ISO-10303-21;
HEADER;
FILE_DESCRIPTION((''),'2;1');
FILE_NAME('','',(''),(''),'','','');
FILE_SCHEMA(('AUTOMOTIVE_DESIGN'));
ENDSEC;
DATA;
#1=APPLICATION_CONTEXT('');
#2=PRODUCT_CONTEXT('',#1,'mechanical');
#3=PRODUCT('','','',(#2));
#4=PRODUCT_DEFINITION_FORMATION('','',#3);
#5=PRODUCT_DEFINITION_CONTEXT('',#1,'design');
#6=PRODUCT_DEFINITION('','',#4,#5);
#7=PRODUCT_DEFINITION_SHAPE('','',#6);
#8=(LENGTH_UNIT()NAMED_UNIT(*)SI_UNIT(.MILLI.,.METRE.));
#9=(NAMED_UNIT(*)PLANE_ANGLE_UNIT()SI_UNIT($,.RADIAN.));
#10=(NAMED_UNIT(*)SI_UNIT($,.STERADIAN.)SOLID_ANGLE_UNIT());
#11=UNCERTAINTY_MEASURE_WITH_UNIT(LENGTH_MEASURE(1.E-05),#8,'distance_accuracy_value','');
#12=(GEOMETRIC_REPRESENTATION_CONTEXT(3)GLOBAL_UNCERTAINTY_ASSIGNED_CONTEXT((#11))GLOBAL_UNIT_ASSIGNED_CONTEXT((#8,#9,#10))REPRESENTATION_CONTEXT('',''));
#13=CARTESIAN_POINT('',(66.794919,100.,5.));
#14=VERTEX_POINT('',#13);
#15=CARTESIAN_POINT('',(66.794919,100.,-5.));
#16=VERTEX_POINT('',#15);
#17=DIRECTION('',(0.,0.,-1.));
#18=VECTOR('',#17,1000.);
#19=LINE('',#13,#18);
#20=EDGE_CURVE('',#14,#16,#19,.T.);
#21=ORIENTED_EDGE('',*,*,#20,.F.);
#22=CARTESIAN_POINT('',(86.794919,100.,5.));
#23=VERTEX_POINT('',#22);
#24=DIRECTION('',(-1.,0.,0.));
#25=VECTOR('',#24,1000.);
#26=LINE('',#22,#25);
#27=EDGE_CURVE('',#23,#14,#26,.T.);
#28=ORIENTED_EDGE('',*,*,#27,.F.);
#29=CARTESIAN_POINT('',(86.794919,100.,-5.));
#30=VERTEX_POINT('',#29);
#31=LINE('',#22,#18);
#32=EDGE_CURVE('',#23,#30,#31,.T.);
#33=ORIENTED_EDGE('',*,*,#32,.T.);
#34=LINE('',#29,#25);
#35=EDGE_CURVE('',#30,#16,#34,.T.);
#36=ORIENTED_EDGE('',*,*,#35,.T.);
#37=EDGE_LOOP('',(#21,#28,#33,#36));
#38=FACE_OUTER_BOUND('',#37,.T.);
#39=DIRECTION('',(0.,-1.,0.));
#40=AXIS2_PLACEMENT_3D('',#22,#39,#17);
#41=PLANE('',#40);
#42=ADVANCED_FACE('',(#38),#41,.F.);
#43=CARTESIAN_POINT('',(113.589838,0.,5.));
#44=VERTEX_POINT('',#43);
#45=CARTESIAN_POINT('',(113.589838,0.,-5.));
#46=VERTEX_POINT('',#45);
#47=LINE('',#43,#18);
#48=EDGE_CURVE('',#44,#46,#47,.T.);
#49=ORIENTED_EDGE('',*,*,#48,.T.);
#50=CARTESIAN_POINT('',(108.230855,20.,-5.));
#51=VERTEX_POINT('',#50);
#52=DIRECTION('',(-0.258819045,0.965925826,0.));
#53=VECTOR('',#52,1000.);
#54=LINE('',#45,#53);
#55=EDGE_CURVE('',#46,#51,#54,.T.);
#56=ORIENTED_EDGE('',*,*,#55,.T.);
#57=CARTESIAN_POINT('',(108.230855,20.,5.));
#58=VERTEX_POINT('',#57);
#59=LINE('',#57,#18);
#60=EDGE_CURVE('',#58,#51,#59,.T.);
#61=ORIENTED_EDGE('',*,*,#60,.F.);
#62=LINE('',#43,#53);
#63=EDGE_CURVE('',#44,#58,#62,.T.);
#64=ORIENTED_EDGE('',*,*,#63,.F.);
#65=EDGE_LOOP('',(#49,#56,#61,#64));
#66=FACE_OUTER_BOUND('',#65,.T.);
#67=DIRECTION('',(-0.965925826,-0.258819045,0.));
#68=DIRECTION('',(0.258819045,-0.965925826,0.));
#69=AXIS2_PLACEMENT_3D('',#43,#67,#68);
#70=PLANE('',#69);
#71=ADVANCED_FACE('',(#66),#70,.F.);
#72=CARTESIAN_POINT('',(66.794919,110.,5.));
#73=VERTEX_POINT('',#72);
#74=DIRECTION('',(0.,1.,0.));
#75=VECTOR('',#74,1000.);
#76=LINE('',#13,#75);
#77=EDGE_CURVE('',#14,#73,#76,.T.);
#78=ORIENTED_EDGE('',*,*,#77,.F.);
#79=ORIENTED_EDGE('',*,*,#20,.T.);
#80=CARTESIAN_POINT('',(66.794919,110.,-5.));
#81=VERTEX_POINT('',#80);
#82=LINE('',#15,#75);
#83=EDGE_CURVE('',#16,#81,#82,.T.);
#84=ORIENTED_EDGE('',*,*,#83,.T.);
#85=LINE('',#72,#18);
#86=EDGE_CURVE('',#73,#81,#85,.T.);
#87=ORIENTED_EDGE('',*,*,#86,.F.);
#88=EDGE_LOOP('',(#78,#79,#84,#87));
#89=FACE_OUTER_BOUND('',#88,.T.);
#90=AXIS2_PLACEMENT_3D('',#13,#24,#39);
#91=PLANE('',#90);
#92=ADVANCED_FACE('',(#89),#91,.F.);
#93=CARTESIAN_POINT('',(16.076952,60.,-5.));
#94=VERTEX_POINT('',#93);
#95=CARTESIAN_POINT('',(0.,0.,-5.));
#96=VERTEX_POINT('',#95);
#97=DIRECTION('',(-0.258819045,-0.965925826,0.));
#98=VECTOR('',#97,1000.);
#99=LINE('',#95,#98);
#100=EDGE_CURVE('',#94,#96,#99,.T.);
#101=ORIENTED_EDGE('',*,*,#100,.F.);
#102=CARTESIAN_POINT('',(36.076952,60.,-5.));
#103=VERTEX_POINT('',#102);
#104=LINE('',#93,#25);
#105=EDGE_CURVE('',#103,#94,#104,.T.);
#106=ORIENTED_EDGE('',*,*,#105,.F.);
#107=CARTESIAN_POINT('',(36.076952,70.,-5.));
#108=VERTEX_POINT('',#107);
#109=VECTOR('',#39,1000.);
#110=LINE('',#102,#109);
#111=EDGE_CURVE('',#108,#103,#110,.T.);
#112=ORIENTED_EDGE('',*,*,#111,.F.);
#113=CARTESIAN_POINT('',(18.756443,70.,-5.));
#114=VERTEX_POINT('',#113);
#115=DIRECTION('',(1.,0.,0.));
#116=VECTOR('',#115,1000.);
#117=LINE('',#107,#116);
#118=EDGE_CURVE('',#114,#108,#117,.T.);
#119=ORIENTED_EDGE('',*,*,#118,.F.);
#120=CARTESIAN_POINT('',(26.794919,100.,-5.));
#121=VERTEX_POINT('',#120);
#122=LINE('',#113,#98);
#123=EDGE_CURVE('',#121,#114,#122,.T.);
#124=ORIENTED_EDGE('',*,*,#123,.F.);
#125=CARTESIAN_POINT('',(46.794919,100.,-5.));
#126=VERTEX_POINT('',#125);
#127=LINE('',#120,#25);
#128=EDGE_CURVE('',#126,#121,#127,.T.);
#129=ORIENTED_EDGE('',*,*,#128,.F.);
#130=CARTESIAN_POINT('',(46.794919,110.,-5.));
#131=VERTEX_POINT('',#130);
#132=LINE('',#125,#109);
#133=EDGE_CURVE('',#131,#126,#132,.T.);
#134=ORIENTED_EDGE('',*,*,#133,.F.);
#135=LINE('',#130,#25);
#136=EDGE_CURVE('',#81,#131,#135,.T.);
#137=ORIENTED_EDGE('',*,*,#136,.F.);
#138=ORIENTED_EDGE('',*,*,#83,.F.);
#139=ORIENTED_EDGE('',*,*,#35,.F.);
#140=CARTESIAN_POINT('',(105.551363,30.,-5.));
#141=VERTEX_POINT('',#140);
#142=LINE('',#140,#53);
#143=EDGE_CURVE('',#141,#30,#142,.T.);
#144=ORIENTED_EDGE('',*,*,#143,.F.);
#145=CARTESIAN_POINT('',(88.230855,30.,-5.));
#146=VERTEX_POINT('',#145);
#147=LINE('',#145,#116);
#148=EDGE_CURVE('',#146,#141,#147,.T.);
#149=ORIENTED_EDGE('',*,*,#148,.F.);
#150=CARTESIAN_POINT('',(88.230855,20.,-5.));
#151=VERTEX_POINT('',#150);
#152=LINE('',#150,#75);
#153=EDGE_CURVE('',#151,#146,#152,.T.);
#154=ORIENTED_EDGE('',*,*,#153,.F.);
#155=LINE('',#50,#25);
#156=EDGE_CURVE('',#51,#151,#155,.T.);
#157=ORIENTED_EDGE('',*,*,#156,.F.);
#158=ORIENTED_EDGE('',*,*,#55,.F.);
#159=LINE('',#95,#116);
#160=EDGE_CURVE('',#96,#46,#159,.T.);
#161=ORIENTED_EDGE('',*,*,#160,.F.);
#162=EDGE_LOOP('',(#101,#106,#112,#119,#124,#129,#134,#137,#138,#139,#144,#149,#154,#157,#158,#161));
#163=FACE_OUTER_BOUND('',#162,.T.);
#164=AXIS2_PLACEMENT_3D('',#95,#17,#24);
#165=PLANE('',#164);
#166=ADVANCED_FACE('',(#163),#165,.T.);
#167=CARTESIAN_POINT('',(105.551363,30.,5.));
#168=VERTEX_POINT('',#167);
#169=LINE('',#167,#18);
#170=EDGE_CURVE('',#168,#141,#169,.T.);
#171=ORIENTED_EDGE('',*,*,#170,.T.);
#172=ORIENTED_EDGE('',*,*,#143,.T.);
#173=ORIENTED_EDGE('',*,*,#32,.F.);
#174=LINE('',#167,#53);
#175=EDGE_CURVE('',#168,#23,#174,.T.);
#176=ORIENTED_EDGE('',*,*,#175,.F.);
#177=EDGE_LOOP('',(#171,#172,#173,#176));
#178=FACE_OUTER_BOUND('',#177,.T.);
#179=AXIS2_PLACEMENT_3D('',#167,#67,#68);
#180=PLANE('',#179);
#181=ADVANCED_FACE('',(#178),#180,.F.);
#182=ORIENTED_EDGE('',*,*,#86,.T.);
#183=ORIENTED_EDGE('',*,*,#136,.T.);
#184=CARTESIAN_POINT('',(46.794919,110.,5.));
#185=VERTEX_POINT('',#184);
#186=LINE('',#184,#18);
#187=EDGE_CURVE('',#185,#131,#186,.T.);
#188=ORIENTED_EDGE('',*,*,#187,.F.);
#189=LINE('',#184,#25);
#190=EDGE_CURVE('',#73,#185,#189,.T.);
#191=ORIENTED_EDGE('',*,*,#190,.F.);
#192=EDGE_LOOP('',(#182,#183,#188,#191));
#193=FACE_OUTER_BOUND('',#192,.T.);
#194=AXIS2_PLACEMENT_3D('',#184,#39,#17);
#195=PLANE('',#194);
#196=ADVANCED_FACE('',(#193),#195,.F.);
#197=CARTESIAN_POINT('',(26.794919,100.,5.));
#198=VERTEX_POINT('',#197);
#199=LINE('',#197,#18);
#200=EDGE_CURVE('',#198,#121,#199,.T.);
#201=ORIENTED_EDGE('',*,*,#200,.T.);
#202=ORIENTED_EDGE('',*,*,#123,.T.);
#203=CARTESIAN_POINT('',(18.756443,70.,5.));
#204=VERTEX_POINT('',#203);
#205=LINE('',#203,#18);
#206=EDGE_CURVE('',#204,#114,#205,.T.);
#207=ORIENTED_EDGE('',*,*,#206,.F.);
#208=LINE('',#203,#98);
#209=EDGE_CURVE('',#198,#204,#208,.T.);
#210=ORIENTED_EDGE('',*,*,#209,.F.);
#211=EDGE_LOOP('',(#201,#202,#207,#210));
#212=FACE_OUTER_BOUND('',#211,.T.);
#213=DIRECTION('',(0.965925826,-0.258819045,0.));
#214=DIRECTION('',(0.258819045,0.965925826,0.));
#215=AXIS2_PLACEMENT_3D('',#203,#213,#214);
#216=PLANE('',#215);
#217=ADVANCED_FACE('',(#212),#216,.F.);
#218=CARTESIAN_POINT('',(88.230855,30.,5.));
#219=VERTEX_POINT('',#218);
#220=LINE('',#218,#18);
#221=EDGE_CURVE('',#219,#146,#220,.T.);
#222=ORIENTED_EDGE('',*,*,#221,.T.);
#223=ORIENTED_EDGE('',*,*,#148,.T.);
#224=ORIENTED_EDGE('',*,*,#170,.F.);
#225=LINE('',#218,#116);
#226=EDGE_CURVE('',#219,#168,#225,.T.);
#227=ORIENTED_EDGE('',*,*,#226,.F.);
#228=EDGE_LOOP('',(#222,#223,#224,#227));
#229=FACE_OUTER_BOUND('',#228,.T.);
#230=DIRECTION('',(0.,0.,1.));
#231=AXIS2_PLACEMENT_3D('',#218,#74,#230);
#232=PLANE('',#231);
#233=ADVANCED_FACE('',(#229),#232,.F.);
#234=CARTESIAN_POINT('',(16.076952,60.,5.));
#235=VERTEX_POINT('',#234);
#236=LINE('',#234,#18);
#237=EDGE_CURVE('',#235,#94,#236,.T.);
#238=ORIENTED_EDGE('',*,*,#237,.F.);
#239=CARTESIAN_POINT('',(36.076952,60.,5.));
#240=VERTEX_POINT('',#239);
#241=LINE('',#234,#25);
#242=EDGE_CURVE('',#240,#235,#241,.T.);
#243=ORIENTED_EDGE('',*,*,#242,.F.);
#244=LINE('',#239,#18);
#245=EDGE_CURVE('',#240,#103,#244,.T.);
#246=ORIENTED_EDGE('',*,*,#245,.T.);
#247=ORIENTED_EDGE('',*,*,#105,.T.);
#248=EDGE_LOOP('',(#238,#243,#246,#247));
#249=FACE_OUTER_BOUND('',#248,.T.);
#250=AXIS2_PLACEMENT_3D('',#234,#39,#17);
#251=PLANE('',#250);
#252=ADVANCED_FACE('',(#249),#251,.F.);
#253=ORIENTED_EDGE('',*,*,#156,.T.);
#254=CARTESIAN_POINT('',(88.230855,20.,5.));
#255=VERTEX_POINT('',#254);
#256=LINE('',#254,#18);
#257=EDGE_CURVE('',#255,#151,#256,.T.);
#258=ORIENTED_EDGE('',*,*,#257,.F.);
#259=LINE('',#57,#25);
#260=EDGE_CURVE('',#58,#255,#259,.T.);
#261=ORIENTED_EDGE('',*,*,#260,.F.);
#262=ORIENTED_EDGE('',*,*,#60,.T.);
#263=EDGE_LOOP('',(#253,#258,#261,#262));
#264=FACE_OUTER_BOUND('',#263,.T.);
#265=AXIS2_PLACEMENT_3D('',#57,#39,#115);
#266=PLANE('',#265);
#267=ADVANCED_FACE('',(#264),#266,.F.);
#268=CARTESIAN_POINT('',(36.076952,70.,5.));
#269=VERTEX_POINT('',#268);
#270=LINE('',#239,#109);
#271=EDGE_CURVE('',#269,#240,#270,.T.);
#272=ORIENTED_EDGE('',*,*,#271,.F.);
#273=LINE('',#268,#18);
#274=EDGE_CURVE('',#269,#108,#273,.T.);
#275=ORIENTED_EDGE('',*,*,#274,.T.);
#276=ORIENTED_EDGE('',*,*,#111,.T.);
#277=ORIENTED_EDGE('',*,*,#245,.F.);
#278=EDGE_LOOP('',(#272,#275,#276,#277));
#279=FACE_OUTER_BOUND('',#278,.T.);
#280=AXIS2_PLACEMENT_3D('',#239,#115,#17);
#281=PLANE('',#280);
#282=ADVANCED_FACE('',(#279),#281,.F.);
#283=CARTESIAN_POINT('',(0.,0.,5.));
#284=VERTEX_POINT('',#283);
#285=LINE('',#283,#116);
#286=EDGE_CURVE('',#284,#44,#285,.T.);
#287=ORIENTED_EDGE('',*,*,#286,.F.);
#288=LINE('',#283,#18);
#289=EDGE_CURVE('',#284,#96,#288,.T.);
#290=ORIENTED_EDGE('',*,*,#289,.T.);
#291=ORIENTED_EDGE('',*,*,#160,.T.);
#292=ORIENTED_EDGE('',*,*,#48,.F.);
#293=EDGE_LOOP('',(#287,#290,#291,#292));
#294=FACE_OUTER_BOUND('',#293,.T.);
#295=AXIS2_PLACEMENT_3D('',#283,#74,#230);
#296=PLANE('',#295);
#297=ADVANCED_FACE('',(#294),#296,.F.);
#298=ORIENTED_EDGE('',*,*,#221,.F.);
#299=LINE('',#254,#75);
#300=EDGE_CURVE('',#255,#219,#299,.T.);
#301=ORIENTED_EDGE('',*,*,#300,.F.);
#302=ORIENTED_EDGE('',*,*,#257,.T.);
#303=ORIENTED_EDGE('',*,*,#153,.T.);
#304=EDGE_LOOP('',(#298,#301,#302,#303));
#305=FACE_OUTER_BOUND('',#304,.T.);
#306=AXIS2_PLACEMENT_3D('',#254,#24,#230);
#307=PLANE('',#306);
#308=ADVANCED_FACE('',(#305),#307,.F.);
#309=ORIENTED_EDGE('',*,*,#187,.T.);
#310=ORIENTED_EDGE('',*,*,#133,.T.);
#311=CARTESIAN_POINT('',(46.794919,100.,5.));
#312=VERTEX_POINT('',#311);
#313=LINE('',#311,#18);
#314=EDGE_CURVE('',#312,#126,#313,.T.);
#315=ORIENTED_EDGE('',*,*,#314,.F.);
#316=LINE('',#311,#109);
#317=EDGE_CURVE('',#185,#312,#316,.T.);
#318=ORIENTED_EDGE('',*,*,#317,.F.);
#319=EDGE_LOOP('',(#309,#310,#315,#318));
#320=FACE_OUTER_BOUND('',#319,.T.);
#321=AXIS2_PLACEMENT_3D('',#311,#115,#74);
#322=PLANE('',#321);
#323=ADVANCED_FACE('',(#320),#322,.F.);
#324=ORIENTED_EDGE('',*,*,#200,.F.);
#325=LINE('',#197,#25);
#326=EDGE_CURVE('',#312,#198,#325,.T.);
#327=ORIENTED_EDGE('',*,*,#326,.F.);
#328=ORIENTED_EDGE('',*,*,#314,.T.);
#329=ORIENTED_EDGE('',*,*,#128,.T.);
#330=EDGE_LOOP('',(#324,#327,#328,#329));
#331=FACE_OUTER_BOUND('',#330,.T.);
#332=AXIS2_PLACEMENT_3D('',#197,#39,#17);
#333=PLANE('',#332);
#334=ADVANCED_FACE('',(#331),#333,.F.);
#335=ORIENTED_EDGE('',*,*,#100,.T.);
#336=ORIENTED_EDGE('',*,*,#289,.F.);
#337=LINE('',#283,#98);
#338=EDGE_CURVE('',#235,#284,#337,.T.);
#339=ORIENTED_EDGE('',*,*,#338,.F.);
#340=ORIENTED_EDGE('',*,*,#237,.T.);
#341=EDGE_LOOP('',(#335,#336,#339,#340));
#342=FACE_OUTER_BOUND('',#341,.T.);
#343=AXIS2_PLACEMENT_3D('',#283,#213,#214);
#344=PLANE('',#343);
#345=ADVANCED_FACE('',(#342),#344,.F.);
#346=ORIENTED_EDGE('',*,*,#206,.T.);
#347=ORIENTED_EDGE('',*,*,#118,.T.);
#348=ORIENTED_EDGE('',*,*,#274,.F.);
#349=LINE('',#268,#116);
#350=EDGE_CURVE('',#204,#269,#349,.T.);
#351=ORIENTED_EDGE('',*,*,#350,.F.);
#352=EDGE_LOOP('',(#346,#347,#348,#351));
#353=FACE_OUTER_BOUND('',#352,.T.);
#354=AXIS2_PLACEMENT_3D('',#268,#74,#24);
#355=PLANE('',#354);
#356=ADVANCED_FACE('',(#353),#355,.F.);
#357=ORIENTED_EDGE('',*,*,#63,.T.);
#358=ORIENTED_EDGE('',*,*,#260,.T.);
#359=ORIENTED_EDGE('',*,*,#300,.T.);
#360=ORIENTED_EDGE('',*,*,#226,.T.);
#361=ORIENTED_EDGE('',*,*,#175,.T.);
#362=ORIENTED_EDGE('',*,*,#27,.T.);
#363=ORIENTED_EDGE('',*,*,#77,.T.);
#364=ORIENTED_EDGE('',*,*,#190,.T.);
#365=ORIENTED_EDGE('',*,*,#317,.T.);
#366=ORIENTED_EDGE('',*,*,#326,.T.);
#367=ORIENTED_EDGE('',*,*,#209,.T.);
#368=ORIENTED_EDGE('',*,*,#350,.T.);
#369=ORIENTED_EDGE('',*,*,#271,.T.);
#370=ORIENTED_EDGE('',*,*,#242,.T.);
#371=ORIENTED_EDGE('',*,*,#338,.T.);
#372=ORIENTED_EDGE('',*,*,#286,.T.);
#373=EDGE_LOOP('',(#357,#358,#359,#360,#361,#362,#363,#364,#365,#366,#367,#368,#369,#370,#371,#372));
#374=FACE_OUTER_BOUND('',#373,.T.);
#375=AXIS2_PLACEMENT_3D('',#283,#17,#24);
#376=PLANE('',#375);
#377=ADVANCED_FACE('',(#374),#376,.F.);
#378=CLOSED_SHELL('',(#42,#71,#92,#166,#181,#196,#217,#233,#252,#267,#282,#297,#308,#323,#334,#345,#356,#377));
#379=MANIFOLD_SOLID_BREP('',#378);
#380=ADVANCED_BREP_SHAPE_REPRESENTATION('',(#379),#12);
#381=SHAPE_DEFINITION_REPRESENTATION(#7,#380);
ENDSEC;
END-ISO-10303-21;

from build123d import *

# Parameters (mm, degrees)
LEG_PLATE_10MM_DEPTH = 5


with BuildPart() as part:
    # Leg Profile Sketch → Leg Plate 10mm (new, symmetric)
    with BuildSketch(Plane.XY):
        Polygon((0, 0), (113.589838486, 0), (108.230854638, 20), (88.230854638, 20), (88.230854638, 30), (105.551362713, 30), (86.794919243, 100), (66.794919243, 100), (66.794919243, 110), (46.794919243, 110), (46.794919243, 100), (26.794919243, 100), (18.75644347, 70), (36.076951546, 70), (36.076951546, 60), (16.076951546, 60), align=None)
    extrude(amount=LEG_PLATE_10MM_DEPTH, both=True)


solid = part.part
